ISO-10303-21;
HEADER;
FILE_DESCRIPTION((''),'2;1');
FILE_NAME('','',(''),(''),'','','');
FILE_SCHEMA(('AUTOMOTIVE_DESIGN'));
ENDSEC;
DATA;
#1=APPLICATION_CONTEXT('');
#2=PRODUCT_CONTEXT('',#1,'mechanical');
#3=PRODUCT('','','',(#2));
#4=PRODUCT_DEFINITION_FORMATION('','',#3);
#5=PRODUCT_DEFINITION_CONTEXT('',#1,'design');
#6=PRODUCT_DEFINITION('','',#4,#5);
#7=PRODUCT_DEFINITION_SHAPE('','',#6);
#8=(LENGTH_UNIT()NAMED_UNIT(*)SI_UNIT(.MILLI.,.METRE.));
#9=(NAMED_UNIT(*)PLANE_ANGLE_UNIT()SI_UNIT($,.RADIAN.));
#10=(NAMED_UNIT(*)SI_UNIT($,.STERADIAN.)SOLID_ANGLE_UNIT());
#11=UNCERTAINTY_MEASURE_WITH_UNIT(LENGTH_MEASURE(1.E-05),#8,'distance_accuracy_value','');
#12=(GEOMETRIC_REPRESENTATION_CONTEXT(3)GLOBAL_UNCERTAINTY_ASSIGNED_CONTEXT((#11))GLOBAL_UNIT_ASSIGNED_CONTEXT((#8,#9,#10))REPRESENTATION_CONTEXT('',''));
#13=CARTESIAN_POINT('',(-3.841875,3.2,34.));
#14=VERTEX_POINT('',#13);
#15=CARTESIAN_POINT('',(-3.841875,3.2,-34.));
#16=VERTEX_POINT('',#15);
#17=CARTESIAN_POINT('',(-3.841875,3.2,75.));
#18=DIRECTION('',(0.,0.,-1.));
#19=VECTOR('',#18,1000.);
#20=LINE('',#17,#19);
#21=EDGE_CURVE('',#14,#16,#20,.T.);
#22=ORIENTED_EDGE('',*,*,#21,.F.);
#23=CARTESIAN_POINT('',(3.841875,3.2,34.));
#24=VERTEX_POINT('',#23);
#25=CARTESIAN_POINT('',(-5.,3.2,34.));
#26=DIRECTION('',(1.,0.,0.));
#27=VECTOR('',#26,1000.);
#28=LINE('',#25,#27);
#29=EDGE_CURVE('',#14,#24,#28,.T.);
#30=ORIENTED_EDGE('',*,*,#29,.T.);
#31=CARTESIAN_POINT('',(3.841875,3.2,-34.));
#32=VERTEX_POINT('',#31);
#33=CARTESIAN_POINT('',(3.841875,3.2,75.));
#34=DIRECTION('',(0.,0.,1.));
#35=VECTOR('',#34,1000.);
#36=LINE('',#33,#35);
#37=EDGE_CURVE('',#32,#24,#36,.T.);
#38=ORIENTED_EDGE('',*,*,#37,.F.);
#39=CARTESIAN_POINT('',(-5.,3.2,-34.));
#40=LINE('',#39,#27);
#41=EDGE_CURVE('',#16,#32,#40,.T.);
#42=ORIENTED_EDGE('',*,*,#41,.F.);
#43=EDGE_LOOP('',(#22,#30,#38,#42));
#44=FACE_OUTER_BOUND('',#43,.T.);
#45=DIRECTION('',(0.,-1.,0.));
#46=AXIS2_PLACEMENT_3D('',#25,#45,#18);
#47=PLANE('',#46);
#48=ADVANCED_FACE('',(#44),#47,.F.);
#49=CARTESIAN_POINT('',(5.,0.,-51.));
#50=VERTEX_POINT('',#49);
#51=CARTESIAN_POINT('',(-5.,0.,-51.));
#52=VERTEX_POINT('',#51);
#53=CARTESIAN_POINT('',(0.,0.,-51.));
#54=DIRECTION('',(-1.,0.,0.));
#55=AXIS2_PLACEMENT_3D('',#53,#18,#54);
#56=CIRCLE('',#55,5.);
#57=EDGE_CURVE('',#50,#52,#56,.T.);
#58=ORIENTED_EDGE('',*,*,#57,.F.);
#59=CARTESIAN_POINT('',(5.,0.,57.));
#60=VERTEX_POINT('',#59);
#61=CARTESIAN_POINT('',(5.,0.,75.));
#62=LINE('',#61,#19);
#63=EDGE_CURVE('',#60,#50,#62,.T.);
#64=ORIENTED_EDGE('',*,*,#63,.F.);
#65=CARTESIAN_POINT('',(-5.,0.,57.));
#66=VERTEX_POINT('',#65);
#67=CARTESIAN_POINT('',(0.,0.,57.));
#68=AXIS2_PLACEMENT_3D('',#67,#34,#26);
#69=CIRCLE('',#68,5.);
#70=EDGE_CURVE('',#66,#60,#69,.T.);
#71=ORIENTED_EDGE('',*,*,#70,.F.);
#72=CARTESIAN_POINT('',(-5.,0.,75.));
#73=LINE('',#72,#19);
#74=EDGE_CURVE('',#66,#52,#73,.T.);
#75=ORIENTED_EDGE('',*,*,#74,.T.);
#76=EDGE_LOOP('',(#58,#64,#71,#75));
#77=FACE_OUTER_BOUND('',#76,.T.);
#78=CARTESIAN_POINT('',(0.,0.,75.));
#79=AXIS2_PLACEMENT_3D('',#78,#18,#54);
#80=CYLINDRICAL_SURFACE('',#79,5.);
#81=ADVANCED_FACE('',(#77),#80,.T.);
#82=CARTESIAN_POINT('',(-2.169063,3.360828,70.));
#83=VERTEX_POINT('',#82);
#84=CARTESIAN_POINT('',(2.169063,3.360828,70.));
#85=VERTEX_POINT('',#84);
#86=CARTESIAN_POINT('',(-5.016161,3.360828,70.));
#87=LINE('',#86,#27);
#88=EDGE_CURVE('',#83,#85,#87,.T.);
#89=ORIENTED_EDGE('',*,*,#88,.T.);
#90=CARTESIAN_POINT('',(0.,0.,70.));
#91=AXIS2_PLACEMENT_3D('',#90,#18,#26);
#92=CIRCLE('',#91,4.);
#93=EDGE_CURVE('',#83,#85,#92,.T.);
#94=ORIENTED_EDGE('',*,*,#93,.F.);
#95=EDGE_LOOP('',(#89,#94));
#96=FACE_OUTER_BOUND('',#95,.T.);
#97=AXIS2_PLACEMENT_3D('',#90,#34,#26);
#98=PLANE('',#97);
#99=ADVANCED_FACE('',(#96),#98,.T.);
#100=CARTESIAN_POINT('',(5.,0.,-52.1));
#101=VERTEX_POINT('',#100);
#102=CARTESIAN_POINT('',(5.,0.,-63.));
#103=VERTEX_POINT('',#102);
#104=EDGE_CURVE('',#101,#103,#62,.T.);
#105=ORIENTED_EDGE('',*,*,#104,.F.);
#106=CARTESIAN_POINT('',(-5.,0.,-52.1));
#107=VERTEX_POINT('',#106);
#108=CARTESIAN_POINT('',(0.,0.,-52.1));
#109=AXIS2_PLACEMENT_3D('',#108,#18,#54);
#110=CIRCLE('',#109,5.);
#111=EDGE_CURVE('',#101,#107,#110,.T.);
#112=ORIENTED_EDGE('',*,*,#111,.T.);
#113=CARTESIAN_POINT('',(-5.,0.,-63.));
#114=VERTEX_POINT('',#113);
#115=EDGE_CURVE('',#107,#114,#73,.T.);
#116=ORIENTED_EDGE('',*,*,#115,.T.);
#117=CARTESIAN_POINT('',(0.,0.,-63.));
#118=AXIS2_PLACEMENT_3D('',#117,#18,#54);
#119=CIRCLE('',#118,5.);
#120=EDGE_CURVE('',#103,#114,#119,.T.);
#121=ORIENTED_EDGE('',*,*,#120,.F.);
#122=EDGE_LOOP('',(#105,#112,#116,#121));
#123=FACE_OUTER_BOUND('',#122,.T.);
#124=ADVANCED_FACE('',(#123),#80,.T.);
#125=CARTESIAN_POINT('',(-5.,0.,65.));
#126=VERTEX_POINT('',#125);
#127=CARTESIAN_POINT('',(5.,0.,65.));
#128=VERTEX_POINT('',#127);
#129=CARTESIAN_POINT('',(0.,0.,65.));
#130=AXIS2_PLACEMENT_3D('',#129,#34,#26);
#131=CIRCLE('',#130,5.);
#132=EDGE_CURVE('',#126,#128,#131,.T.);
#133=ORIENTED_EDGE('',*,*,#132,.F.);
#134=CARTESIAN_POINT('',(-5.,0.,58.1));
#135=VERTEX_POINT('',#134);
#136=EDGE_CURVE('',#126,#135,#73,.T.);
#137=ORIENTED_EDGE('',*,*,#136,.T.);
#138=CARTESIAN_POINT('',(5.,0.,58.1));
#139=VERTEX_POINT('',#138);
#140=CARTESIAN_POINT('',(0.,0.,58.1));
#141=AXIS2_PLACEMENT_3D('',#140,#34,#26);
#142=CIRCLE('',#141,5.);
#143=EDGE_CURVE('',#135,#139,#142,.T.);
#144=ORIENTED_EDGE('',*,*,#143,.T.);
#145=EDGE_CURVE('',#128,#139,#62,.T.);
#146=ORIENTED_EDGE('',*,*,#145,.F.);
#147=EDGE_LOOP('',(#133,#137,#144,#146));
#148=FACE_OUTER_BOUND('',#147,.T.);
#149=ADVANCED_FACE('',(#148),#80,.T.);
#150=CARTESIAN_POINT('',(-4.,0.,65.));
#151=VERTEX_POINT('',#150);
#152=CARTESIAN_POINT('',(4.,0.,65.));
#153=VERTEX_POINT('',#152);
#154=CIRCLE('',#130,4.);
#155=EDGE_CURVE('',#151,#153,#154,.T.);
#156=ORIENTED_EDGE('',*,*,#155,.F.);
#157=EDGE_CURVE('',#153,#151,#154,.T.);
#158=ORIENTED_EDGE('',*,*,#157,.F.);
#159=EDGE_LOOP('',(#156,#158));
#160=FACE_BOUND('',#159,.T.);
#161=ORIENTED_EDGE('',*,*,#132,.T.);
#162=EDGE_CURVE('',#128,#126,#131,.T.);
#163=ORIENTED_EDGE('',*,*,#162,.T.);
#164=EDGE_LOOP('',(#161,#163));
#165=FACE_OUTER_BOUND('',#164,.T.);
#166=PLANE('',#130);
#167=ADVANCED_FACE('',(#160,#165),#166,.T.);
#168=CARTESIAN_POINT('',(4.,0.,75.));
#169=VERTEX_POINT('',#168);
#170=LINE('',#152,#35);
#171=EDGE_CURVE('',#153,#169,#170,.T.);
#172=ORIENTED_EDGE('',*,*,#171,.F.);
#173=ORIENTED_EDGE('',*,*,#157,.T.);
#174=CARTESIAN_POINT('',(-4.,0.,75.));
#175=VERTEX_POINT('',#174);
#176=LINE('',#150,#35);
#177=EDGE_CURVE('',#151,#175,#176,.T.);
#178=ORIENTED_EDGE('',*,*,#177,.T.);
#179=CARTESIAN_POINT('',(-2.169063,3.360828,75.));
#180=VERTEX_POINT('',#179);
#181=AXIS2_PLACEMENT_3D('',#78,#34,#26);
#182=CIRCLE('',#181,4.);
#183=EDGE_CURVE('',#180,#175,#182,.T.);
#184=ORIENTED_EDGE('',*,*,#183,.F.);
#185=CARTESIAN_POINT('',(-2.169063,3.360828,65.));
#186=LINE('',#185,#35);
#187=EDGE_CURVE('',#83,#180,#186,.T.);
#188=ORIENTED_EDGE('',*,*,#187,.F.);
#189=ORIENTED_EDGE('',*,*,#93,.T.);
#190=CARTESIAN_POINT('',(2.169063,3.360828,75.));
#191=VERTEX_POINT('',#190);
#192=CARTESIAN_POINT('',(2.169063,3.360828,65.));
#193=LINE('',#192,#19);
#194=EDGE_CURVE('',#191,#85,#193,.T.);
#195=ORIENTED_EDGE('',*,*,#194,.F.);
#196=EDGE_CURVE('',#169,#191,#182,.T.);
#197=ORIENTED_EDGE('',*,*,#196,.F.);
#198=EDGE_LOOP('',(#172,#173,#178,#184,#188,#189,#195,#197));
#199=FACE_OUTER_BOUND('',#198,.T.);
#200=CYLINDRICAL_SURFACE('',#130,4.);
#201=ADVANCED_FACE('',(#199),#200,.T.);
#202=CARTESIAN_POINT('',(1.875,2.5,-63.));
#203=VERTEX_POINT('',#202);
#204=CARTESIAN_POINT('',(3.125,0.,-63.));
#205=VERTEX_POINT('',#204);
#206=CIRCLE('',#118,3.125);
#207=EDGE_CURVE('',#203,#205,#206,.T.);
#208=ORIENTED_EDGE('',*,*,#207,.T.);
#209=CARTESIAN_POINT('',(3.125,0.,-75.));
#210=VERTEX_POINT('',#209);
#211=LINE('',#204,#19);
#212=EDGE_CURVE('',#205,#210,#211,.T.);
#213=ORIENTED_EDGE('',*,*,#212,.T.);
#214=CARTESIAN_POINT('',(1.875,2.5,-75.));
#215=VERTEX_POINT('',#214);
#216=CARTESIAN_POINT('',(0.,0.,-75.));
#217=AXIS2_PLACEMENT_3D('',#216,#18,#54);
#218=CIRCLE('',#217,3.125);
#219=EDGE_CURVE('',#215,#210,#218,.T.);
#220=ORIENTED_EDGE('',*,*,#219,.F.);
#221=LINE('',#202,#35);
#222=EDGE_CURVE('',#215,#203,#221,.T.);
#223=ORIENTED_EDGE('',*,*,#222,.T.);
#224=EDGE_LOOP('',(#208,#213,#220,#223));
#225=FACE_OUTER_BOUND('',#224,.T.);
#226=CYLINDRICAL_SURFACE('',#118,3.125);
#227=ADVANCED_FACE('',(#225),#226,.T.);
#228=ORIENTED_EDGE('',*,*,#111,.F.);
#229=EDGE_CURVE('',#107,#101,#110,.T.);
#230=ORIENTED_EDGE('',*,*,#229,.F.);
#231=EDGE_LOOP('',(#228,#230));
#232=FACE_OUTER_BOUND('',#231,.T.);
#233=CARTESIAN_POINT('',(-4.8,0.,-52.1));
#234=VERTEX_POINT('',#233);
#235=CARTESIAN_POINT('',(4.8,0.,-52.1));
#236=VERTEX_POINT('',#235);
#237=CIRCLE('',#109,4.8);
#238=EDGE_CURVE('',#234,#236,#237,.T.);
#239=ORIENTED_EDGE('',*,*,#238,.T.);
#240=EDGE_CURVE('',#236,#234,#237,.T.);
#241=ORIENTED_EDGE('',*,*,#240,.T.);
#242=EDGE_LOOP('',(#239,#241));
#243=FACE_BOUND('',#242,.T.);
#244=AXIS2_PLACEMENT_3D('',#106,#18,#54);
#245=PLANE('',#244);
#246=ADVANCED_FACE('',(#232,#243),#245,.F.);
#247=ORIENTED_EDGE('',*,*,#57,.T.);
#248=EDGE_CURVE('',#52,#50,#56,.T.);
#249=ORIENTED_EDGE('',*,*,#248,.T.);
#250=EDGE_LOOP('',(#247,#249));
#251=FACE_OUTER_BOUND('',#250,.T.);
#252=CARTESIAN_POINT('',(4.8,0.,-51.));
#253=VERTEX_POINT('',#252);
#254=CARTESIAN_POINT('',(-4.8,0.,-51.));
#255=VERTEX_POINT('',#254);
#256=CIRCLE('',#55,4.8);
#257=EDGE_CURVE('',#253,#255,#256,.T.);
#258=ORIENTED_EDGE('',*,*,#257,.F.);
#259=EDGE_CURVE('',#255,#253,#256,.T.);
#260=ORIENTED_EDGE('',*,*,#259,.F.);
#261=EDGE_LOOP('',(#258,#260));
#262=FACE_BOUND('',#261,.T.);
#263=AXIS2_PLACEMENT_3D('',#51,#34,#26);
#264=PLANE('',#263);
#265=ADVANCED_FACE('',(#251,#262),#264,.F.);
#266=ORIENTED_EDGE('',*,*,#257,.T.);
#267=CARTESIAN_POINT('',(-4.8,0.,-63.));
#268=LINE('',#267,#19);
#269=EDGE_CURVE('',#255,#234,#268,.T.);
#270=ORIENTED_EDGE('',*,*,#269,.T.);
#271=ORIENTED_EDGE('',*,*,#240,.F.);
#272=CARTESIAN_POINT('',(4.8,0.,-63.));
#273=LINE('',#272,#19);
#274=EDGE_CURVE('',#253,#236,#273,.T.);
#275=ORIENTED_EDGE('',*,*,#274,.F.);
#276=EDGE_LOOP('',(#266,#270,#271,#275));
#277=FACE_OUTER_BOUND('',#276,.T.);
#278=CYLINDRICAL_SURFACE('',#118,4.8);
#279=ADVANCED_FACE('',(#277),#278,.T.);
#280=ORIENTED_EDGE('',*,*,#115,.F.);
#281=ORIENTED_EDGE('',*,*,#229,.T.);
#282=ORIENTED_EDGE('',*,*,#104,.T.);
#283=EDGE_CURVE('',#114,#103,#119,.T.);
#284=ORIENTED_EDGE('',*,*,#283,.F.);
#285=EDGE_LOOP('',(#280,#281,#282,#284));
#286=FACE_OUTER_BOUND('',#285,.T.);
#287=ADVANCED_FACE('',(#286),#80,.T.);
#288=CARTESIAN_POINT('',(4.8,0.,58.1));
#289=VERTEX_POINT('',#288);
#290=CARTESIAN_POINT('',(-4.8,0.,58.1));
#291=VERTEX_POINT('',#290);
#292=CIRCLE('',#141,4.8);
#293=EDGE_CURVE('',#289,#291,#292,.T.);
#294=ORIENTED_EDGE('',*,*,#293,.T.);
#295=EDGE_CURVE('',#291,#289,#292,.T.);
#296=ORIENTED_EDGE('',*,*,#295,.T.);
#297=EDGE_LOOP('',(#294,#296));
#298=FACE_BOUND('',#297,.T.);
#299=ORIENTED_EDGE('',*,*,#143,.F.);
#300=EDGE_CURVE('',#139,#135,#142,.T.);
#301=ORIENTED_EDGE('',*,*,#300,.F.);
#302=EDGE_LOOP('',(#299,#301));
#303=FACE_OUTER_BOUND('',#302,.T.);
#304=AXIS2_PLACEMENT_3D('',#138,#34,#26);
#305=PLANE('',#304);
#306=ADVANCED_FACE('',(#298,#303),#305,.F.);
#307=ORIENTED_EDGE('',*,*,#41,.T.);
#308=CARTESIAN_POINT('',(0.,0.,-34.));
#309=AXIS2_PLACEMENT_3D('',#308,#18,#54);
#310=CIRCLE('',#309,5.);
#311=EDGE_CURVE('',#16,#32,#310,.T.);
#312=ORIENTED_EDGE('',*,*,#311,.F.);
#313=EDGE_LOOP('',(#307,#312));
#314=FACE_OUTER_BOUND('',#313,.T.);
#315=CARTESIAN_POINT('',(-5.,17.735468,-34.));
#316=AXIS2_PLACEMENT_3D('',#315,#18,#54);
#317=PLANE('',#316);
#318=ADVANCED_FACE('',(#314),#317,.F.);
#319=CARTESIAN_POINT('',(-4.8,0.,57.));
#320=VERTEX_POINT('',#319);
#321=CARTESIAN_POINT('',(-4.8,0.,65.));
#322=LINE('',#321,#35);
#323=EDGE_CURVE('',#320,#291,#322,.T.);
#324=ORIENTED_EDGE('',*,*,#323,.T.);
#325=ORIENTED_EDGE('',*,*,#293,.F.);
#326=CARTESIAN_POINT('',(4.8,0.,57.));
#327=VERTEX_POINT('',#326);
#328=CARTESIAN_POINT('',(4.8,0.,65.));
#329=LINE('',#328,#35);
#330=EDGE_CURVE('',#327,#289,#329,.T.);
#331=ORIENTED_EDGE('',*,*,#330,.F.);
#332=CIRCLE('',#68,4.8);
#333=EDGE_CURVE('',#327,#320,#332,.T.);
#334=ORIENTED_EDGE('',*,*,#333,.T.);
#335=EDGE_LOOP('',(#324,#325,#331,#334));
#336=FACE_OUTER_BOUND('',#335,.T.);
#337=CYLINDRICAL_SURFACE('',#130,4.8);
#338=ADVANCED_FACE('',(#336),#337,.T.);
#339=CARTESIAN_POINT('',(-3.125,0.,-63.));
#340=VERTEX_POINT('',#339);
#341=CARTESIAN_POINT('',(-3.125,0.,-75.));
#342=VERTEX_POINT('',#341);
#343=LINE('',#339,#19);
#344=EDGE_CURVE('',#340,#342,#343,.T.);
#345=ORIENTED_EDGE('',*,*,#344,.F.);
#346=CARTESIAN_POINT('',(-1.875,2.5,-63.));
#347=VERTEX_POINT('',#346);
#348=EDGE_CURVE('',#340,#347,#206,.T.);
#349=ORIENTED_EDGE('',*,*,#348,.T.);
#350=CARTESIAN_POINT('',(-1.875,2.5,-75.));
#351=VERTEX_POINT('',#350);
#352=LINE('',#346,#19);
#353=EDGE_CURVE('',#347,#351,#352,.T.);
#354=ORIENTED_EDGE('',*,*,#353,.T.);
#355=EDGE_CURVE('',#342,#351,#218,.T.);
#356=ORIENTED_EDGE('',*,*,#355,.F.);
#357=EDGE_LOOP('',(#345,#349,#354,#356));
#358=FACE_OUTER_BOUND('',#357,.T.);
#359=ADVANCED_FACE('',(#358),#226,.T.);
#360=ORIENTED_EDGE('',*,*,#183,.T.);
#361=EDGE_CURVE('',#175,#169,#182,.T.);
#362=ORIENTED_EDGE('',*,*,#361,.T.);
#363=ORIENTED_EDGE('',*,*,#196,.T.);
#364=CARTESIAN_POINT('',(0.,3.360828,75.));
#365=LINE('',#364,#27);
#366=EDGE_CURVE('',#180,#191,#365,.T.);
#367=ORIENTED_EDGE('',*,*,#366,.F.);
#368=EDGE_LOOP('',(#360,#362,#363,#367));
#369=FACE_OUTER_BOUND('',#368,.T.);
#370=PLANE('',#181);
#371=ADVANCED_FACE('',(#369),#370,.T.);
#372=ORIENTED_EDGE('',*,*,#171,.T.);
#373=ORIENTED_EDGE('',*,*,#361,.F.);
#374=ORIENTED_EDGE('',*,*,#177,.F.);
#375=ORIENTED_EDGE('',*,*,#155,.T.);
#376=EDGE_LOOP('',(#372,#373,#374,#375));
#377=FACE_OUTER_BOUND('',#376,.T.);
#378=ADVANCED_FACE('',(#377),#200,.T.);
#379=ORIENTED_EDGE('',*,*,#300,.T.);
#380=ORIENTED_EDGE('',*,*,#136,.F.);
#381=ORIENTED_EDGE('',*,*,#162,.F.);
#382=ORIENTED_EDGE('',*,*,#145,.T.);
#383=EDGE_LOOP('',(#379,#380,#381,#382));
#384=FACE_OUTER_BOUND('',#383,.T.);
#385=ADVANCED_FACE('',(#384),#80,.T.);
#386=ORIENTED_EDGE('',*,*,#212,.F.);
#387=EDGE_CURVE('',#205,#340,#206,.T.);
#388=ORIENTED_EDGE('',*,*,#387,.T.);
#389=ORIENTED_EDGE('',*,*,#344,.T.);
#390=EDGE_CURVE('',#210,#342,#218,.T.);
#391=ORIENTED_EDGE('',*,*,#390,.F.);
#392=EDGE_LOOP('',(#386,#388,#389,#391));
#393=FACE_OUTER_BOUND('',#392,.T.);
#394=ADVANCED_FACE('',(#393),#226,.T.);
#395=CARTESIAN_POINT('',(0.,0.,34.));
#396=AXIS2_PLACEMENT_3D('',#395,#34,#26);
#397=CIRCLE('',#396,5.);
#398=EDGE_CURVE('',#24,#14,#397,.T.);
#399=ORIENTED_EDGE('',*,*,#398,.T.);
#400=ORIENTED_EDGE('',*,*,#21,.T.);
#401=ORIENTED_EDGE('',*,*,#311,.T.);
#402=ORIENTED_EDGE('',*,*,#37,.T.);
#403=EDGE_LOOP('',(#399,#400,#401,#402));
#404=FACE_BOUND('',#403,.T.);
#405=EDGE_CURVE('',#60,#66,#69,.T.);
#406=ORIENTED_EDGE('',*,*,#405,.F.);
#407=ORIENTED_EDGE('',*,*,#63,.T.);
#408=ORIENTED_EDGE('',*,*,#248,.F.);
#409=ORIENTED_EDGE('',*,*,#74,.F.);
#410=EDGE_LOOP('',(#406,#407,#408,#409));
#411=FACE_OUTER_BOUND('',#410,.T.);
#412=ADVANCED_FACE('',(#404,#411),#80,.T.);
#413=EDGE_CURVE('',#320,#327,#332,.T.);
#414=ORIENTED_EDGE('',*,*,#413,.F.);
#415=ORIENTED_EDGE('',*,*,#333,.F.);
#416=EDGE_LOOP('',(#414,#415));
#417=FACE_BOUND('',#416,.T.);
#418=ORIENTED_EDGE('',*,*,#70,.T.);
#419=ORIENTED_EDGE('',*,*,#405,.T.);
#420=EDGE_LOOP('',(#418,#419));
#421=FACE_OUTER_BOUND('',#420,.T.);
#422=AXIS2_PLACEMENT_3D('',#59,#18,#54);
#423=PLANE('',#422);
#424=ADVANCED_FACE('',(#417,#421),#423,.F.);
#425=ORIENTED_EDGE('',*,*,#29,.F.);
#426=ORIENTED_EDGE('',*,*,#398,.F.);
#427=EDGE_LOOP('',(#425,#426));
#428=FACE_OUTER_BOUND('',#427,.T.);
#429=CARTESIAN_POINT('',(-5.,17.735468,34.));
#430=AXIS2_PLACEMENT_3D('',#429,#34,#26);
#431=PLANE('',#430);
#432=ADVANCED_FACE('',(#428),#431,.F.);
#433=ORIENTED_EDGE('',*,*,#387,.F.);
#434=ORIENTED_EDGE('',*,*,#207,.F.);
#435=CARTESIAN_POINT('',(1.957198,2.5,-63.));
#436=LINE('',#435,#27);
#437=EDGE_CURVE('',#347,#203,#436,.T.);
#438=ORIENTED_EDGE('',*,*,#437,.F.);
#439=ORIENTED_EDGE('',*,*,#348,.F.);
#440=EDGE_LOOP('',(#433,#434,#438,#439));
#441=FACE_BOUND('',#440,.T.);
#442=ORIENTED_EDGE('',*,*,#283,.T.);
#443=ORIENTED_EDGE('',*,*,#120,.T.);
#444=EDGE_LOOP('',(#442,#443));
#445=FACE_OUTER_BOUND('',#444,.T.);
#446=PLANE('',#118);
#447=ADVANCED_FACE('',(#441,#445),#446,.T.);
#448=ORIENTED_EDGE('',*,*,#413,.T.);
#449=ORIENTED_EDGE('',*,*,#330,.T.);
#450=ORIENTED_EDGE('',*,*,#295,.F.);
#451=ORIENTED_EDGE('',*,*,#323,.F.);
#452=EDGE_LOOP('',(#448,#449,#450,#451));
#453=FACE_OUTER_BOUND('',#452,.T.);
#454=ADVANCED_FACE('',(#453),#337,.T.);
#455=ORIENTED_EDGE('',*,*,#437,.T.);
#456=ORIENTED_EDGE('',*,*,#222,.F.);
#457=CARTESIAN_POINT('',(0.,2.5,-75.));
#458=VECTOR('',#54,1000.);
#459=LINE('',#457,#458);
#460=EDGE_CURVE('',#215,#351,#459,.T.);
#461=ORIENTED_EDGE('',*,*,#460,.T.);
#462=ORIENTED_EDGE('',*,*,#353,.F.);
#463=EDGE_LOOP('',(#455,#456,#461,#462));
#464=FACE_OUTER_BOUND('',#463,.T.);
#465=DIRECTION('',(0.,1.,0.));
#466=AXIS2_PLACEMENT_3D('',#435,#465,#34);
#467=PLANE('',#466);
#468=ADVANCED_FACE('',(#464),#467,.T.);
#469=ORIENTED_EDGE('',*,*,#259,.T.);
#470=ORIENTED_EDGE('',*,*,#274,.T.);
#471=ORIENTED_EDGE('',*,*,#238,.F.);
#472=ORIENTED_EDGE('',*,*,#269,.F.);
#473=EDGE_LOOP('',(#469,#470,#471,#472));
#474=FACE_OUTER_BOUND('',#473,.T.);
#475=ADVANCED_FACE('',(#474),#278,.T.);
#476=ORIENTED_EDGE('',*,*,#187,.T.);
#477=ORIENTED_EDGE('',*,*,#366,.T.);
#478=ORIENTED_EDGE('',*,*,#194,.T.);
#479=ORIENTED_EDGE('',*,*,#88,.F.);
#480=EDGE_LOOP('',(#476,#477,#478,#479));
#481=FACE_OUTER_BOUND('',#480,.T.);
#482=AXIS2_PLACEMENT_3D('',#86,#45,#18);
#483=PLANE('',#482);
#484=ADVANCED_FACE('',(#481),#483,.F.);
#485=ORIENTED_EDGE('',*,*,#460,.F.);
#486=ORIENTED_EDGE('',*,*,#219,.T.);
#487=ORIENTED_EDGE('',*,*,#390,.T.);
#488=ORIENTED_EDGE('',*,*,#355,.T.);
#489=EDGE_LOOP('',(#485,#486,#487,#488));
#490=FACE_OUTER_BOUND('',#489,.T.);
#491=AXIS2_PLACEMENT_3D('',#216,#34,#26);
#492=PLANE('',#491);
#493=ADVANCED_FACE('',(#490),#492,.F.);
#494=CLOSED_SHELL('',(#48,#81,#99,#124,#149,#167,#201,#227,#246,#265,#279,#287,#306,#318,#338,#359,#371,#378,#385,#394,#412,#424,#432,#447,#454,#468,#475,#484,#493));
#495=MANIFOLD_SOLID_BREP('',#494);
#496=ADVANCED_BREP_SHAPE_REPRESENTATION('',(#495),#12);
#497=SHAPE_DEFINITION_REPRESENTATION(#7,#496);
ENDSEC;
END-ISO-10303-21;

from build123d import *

# Parameters (mm, degrees)
SKETCH1_R               = 5
BOSS_EXTRUDE1_DEPTH     = 75
CUT_EXTRUDE1_DEPTH      = 76.332595867
CUT_EXTRUDE1_DEPTH_BACK = 76.332595867
SKETCH2_W               = 68
SKETCH2_H               = 14.535467824
CUT_EXTRUDE2_START      = -12
SKETCH3_R               = 5
SKETCH3_R_2             = 3.125
CUT_EXTRUDE2_DEPTH      = 12
SKETCH4_OUTSIDE_W       = 42.134
SKETCH4_OUTSIDE_H       = 42.134
CUT_EXTRUDE3_DEPTH      = 12
SKETCH5_OUTSIDE_W       = 42.134
SKETCH5_OUTSIDE_H       = 42.134
SKETCH5_OUTSIDE_R       = 4
CUT_EXTRUDE4_DEPTH      = 10
SKETCH6_W               = 10.564036003
SKETCH6_H               = 1.244008039
CUT_EXTRUDE5_DEPTH      = 5
SKETCH31_W              = 1.1
SKETCH31_H              = 0.2
SKETCH32_W              = 1.1
SKETCH32_H              = 0.2


with BuildPart() as part:
    # Sketch1 → Boss-Extrude1 (new, symmetric)
    with BuildSketch(Plane.XY):
        Circle(SKETCH1_R)
    extrude(amount=BOSS_EXTRUDE1_DEPTH, both=True)

    # Sketch2 → Cut-Extrude1 (cut, two sides: drawn at the far end of the back side and taken through both)
    with BuildSketch(Plane(origin=(0, 0, 0), x_dir=(0, 0, -1), z_dir=(1, 0, 0)).offset(-CUT_EXTRUDE1_DEPTH_BACK)):
        with Locations((0, 10.467733912)):
            Rectangle(SKETCH2_W, SKETCH2_H)
    extrude(amount=CUT_EXTRUDE1_DEPTH + CUT_EXTRUDE1_DEPTH_BACK, mode=Mode.SUBTRACT)

    # Sketch3 → Cut-Extrude2 (cut)
    with BuildSketch(Plane(origin=(0, 0, -75), x_dir=(-1, 0, 0), z_dir=(0, 0, -1)).offset(CUT_EXTRUDE2_START)):
        Circle(SKETCH3_R)
        Circle(SKETCH3_R_2, mode=Mode.SUBTRACT)
    extrude(amount=CUT_EXTRUDE2_DEPTH, mode=Mode.SUBTRACT)

    # Sketch4 outside → Cut-Extrude3 (cut)
    with BuildSketch(Plane(origin=(0, 0, -75), x_dir=(-1, 0, 0), z_dir=(0, 0, -1))):
        Rectangle(SKETCH4_OUTSIDE_W, SKETCH4_OUTSIDE_H)
        with BuildLine():
            Line((-1.957198253, 2.5), (1.957198253, 2.5))
            ThreePointArc((1.957198253, 2.5), (0, -3.175), (-1.957198253, 2.5))
        make_face(mode=Mode.SUBTRACT)
    extrude(amount=-CUT_EXTRUDE3_DEPTH, mode=Mode.SUBTRACT)

    # Sketch5 outside → Cut-Extrude4 (cut)
    with BuildSketch(Plane.XY.offset(75)):
        Rectangle(SKETCH5_OUTSIDE_W, SKETCH5_OUTSIDE_H)
        Circle(SKETCH5_OUTSIDE_R, mode=Mode.SUBTRACT)
    extrude(amount=-CUT_EXTRUDE4_DEPTH, mode=Mode.SUBTRACT)

    # Sketch6 → Cut-Extrude5 (cut)
    with BuildSketch(Plane.XY.offset(75)):
        with Locations((0.265856556, 3.982832188)):
            Rectangle(SKETCH6_W, SKETCH6_H)
    extrude(amount=-CUT_EXTRUDE5_DEPTH, mode=Mode.SUBTRACT)

    # Sketch31 → Cut-Revolve1 (revolve, cut)
    with BuildSketch(Plane(origin=(-100, 0, -63), x_dir=(0, 0, 1), z_dir=(0, 1, 0))):
        with Locations((11.45, 95.1)):
            Rectangle(SKETCH31_W, SKETCH31_H)
    revolve(axis=Axis((0, 0, -63), (0, 0, 1)), mode=Mode.SUBTRACT)

    # Sketch32 → Cut-Revolve11 (revolve, cut)
    with BuildSketch(Plane(origin=(100, 0, 65), x_dir=(0, 0, -1), z_dir=(0, 1, 0)), mode=Mode.PRIVATE) as cut_revolve11_sk:
        with Locations((7.45, 95.1)):
            Rectangle(SKETCH32_W, SKETCH32_H)
    revolve(cut_revolve11_sk.sketch.rotate(Axis((0, 0, 65), (0, 0, -1)), 180), axis=Axis((0, 0, 65), (0, 0, -1)), mode=Mode.SUBTRACT)


solid = part.part
